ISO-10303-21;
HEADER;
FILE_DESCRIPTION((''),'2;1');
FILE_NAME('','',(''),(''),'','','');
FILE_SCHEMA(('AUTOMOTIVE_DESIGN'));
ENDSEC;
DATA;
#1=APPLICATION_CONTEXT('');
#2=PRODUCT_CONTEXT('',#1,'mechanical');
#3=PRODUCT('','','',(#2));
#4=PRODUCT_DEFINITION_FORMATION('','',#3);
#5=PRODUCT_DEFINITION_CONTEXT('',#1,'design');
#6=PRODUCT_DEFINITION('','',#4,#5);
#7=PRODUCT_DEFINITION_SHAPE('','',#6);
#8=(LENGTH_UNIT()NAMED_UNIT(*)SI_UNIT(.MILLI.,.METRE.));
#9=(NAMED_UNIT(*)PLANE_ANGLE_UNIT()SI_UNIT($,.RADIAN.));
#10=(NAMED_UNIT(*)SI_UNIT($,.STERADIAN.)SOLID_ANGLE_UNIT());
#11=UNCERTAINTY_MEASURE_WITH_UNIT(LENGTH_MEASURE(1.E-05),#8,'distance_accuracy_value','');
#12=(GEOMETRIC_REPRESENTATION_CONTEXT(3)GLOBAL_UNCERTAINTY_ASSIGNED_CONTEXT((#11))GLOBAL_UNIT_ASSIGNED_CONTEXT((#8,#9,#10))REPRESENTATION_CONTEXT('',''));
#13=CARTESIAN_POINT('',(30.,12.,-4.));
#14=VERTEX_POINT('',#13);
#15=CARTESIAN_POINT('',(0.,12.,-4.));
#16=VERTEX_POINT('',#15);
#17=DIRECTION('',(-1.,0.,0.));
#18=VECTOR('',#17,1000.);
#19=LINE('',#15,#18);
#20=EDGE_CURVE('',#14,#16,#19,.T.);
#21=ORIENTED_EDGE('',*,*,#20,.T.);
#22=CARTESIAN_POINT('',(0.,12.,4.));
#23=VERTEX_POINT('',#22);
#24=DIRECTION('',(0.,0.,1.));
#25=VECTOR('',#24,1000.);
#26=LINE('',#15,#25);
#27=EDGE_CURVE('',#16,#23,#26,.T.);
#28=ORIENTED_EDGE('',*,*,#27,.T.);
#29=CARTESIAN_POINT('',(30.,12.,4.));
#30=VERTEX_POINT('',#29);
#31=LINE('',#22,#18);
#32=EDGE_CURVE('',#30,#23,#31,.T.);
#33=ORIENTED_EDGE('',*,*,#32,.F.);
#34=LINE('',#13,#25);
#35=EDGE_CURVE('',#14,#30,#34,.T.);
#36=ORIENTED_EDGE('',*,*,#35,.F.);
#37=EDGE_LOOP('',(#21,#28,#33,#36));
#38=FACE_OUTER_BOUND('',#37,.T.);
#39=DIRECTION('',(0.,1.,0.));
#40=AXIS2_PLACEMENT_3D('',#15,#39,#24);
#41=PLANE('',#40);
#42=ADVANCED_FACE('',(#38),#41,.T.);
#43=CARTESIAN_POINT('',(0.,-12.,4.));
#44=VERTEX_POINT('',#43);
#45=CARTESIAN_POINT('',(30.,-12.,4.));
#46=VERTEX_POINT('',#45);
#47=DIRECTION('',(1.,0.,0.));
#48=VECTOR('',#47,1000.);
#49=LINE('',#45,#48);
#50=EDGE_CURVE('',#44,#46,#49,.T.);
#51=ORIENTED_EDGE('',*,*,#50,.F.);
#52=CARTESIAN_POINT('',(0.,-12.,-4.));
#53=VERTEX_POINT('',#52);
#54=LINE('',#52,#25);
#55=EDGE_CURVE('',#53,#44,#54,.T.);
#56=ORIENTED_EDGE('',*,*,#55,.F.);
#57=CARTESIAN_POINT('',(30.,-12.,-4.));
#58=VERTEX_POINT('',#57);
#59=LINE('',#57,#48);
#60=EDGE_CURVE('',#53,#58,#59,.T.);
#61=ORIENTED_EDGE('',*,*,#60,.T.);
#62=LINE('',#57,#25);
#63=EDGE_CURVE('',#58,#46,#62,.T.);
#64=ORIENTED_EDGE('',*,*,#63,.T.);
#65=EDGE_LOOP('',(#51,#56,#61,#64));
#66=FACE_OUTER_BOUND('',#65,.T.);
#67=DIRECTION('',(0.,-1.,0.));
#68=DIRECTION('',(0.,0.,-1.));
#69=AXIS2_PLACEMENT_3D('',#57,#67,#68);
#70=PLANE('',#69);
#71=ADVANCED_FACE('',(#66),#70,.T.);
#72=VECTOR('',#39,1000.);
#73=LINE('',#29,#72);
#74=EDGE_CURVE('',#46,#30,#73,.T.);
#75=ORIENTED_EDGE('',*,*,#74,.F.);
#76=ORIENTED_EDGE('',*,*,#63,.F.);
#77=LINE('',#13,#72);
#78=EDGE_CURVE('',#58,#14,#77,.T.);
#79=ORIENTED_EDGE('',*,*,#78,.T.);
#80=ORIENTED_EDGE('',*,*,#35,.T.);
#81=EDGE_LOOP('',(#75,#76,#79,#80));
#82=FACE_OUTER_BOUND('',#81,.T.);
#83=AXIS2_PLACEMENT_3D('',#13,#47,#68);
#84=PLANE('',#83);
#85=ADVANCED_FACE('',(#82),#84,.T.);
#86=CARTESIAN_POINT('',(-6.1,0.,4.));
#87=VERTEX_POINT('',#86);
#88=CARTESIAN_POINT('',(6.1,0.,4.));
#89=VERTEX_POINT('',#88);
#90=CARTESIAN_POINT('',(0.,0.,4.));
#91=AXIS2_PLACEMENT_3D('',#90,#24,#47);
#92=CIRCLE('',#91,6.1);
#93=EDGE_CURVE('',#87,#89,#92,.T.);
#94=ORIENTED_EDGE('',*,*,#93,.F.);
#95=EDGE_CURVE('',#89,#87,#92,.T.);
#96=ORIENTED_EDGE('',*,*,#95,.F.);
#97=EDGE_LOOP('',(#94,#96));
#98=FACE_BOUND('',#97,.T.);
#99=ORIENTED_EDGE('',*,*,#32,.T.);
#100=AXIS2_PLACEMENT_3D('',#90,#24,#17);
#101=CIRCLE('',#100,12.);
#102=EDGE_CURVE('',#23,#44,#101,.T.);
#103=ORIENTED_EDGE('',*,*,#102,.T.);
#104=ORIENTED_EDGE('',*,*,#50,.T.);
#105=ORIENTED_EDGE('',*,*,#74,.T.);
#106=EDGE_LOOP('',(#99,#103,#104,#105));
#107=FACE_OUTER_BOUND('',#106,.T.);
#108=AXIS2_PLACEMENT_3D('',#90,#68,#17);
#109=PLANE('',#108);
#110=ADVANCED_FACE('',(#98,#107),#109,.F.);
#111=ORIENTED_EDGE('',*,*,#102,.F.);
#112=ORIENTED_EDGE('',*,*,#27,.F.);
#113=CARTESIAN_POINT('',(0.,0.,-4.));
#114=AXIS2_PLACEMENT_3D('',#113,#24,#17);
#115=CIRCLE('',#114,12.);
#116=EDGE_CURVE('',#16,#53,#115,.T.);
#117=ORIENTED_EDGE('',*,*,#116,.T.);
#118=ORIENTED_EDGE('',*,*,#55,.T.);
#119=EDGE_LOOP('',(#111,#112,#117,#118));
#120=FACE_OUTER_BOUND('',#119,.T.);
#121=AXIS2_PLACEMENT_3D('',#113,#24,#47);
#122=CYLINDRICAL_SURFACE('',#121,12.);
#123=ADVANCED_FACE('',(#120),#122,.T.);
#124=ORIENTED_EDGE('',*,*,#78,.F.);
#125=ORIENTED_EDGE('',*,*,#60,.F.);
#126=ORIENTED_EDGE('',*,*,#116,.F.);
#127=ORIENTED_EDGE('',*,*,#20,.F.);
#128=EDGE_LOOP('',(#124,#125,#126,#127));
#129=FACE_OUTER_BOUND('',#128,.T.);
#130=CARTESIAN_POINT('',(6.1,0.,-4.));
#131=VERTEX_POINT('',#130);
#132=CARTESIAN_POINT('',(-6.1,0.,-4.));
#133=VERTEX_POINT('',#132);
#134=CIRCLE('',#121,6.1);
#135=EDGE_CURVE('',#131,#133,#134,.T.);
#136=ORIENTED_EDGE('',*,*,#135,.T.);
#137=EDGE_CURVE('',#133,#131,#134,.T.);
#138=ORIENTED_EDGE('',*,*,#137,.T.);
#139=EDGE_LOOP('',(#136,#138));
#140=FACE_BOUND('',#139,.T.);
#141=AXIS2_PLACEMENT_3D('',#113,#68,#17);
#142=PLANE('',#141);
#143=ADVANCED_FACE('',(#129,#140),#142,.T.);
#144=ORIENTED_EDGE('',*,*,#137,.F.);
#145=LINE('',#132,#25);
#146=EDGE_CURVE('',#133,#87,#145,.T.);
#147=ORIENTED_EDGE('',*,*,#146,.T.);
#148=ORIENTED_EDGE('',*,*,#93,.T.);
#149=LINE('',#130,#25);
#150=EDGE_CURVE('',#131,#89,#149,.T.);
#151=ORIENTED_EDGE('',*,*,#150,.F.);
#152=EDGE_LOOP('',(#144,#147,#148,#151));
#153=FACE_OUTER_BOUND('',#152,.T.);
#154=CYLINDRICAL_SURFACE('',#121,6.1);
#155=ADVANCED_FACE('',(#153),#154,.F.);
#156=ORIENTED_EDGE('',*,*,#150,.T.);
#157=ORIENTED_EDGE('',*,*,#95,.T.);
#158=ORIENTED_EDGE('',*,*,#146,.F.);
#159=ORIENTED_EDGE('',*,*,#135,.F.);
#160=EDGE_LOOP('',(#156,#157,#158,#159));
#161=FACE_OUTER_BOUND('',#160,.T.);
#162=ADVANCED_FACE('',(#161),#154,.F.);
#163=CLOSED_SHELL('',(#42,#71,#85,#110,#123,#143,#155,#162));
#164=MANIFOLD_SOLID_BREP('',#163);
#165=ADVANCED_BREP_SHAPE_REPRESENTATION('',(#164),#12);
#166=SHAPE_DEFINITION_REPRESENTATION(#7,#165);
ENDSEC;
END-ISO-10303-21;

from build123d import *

# Parameters (mm, degrees)
SKETCH_1_R      = 6.1
EXTRUDE_1_DEPTH = 4


with BuildPart() as part:
    # 草图1 → 凸台-拉伸1 (new, symmetric)
    with BuildSketch(Plane.XY):
        with BuildLine():
            Line((0, 12), (30, 12))
            Line((30, 12), (30, -12))
            Line((30, -12), (0, -12))
            ThreePointArc((0, -12), (-12, 0), (0, 12))
        make_face()
        Circle(SKETCH_1_R, mode=Mode.SUBTRACT)
    extrude(amount=EXTRUDE_1_DEPTH, both=True)


solid = part.part
